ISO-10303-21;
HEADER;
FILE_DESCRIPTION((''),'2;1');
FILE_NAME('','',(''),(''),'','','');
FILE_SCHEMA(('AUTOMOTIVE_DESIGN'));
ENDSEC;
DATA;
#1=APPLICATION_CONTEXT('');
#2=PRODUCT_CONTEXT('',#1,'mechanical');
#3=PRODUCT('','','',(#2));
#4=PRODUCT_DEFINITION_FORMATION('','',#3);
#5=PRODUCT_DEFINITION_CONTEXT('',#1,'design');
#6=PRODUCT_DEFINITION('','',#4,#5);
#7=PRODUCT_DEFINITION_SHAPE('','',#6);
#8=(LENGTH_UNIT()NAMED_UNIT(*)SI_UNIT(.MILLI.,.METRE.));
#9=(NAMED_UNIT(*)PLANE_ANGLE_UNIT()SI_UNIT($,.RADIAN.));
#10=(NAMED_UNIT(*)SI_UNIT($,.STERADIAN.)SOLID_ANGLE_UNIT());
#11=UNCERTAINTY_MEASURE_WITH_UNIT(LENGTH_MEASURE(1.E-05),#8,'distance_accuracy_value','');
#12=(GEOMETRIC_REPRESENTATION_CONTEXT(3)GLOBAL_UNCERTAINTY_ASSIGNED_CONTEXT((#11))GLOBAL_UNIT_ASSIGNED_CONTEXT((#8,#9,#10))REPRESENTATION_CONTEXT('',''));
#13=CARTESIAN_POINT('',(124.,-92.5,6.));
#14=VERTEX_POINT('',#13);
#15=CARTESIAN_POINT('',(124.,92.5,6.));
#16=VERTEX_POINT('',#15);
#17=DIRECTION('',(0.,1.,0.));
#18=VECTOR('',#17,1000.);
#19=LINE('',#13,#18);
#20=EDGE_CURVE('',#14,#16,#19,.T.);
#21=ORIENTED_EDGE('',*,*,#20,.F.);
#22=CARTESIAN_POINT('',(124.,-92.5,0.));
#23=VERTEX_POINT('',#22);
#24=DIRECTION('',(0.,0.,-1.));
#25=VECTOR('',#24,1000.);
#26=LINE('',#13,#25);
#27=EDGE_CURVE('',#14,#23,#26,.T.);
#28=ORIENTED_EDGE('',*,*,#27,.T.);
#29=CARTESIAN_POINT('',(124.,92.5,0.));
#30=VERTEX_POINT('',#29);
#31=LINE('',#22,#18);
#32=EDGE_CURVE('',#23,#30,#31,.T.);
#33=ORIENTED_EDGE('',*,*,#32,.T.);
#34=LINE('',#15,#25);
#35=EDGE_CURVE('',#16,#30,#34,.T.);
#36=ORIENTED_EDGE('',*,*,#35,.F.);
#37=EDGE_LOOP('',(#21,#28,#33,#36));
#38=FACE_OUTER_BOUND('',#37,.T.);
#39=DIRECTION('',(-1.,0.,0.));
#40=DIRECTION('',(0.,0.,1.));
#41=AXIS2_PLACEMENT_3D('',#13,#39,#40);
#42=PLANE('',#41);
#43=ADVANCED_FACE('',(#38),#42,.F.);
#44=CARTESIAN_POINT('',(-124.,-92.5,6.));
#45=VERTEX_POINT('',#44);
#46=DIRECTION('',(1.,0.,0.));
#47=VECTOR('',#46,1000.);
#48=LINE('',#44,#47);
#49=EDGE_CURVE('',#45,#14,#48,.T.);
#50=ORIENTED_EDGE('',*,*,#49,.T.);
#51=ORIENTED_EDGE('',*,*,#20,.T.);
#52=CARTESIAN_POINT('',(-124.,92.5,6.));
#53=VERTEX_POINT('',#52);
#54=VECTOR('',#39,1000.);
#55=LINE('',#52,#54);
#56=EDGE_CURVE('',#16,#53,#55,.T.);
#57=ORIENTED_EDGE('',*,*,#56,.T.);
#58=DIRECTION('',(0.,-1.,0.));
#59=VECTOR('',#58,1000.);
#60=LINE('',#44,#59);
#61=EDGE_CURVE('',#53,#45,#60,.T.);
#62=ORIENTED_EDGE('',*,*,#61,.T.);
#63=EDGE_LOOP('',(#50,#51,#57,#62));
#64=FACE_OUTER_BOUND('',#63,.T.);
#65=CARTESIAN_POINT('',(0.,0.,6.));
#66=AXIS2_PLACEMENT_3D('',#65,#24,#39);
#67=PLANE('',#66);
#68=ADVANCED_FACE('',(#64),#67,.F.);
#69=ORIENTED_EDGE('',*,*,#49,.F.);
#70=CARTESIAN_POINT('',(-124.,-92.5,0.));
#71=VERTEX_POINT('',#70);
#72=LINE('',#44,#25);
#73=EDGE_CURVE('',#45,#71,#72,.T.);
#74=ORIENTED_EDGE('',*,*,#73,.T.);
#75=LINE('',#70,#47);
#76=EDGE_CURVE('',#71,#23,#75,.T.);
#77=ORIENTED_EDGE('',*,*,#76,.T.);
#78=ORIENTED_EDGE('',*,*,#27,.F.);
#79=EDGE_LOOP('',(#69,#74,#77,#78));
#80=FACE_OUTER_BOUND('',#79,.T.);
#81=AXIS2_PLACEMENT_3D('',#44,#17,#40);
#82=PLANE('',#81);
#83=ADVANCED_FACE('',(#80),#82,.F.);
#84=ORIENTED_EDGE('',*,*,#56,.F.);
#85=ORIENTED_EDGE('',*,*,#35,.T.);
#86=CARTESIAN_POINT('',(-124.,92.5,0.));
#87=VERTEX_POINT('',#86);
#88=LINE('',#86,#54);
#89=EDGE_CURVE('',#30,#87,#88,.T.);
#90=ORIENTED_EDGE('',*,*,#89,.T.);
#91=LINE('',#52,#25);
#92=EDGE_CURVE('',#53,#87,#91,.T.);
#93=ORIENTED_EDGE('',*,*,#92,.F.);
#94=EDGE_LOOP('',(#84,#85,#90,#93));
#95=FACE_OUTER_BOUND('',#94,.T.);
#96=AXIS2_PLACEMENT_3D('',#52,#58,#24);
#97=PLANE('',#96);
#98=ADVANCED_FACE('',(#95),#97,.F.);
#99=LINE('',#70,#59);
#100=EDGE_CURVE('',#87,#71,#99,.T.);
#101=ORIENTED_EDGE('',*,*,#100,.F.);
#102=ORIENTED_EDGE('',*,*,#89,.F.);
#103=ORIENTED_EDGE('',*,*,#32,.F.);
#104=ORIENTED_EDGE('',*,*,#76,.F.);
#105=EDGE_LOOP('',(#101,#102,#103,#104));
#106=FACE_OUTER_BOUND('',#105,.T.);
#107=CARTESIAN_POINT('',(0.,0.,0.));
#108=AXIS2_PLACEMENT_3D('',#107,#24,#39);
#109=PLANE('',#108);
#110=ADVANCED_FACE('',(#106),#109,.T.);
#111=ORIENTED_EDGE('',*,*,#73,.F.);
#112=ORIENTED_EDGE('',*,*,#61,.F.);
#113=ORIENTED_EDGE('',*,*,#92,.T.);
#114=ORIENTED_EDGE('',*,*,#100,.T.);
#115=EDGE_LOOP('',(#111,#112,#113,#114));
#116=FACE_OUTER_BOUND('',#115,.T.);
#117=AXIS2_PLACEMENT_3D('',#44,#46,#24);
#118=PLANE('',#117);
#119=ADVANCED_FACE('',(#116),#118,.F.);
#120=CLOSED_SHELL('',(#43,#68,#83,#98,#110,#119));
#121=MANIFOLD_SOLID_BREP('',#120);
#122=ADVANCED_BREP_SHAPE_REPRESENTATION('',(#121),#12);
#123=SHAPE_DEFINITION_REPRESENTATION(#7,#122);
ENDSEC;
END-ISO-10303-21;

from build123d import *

# Parameters (mm, degrees)
SKETCH_1_W      = 248
SKETCH_1_H      = 185
EXTRUDE_1_DEPTH = 6


with BuildPart() as part:
    # 草图1 → 凸台-拉伸1 (new body)
    with BuildSketch(Plane.XY):
        Rectangle(SKETCH_1_W, SKETCH_1_H)
    extrude(amount=EXTRUDE_1_DEPTH)


solid = part.part
